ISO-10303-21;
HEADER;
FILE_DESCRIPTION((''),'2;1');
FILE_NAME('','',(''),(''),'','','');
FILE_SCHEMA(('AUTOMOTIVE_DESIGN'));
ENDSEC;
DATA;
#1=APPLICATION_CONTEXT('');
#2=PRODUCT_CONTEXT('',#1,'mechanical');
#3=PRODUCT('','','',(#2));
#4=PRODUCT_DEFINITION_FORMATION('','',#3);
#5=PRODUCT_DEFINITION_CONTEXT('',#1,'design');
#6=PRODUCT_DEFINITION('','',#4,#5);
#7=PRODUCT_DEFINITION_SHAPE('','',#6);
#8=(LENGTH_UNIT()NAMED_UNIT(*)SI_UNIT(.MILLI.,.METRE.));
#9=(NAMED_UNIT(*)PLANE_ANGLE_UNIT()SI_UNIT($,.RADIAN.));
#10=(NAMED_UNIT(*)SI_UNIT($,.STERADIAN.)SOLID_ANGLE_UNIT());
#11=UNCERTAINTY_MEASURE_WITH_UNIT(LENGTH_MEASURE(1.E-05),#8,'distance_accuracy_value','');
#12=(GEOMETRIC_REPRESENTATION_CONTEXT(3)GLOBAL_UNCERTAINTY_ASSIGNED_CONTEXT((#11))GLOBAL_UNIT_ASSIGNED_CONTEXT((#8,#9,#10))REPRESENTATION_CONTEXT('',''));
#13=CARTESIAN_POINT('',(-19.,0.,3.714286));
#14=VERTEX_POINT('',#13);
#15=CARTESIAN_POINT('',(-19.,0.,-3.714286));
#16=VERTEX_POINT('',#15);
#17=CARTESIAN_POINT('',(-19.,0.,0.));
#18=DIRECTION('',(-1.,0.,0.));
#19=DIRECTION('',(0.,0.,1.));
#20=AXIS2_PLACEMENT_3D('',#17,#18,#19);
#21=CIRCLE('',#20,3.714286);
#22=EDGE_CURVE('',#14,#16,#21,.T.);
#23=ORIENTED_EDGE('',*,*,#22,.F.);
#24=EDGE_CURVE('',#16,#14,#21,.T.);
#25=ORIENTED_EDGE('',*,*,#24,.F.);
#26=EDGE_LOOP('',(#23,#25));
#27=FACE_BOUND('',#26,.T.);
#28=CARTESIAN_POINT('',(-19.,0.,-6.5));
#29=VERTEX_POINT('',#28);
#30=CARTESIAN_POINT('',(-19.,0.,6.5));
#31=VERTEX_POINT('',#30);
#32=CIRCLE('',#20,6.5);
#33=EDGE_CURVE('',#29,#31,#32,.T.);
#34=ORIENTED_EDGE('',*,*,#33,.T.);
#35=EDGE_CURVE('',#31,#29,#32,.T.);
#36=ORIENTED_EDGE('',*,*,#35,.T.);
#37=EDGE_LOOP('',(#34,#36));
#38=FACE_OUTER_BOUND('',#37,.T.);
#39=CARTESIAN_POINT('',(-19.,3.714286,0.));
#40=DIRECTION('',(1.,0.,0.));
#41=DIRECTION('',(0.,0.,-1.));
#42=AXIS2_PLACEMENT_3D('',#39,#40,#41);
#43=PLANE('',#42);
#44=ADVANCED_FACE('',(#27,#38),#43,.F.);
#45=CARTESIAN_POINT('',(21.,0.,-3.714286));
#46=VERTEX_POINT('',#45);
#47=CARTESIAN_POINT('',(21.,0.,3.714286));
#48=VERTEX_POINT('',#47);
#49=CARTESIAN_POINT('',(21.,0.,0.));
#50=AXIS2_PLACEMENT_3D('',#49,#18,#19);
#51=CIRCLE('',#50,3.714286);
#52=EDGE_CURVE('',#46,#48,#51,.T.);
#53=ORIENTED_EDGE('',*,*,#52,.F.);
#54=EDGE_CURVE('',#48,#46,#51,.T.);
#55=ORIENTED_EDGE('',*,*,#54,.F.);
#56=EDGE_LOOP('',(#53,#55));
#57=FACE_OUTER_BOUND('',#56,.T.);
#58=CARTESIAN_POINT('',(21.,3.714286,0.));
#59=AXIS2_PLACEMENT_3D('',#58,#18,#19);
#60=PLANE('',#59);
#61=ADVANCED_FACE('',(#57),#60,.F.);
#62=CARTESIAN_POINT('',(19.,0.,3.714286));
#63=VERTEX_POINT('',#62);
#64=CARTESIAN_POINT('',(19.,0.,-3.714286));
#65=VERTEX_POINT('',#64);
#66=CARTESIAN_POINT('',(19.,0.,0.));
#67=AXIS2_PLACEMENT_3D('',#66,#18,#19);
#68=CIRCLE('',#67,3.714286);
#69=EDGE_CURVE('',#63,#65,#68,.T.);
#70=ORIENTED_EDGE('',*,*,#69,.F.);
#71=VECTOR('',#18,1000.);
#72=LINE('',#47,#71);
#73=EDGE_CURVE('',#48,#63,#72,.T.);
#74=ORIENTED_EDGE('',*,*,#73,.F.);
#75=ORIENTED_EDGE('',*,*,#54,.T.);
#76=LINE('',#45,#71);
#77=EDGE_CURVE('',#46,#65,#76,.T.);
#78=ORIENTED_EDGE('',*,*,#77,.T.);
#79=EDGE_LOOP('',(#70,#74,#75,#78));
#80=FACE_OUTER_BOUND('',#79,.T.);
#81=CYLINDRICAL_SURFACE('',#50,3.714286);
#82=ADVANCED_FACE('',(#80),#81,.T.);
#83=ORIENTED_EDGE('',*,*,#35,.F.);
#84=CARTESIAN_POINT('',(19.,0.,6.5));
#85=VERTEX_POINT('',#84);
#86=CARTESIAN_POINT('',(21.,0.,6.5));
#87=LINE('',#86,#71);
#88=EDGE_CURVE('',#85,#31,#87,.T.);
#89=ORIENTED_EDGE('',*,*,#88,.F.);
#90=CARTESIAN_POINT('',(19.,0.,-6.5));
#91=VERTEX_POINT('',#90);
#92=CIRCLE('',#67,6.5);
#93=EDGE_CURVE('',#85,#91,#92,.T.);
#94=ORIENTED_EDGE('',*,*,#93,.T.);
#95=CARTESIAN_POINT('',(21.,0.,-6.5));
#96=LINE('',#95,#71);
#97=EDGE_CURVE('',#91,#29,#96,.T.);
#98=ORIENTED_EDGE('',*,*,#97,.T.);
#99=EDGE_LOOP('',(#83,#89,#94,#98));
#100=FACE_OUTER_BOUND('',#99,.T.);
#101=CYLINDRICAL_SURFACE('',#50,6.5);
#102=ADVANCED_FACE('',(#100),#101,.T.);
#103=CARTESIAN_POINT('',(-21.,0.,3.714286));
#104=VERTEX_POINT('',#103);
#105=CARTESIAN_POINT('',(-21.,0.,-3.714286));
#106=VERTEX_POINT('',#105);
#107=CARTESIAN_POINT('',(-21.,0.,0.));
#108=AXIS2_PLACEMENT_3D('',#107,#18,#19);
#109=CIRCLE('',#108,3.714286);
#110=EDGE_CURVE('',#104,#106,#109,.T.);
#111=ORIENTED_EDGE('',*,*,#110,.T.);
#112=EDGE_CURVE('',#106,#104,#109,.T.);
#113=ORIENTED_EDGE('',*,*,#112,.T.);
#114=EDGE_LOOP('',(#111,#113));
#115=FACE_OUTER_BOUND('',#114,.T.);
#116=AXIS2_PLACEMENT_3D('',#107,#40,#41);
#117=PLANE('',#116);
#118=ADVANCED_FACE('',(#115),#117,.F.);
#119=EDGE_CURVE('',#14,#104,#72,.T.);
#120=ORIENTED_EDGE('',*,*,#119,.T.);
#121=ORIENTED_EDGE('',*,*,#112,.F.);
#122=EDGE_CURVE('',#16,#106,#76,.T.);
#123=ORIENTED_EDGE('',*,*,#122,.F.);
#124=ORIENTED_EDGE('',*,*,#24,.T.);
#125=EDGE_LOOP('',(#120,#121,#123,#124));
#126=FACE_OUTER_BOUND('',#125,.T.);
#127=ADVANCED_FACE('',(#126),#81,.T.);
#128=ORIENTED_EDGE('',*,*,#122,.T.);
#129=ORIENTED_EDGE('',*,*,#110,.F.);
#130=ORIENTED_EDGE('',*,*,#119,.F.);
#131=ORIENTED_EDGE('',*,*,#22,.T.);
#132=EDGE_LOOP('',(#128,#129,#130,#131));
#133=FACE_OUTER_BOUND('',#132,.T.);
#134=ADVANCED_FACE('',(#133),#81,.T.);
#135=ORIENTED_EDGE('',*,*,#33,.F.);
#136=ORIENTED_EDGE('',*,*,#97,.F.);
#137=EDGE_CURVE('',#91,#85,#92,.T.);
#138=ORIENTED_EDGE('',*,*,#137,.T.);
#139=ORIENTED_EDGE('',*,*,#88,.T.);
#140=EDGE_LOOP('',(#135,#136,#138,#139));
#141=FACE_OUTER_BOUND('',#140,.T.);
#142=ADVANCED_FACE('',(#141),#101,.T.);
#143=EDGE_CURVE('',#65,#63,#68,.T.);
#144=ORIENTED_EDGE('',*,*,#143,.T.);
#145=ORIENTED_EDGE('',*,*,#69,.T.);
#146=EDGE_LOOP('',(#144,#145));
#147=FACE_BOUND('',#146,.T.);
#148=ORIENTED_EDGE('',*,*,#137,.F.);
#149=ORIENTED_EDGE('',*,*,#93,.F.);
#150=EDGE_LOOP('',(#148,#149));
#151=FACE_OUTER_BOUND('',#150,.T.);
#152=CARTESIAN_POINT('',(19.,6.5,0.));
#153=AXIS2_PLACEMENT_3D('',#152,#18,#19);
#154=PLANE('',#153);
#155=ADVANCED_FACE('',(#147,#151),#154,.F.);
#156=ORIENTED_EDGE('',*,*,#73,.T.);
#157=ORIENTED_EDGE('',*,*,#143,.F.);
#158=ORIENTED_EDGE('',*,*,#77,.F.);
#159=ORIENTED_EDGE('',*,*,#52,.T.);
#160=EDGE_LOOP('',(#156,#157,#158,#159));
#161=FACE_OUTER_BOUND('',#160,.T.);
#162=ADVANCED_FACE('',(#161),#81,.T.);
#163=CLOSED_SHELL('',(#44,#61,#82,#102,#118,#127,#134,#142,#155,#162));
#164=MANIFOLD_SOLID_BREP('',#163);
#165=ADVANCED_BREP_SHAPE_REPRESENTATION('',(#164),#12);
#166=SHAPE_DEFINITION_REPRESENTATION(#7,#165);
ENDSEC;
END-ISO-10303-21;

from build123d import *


with BuildPart() as part:
    # 草图1 → 旋转1 (revolve)
    with BuildSketch(Plane.XY, mode=Mode.PRIVATE) as revolve_1_sk:
        Polygon((-21, 0), (-21, 3.714285714), (-19, 3.714285714), (-19, 6.5), (19, 6.5), (19, 3.714285714), (21, 3.714285714), (21, 0), align=None)
    revolve(revolve_1_sk.sketch.rotate(Axis((21, 0, 0), (-1, 0, 0)), 270), axis=Axis((21, 0, 0), (-1, 0, 0)))


solid = part.part
